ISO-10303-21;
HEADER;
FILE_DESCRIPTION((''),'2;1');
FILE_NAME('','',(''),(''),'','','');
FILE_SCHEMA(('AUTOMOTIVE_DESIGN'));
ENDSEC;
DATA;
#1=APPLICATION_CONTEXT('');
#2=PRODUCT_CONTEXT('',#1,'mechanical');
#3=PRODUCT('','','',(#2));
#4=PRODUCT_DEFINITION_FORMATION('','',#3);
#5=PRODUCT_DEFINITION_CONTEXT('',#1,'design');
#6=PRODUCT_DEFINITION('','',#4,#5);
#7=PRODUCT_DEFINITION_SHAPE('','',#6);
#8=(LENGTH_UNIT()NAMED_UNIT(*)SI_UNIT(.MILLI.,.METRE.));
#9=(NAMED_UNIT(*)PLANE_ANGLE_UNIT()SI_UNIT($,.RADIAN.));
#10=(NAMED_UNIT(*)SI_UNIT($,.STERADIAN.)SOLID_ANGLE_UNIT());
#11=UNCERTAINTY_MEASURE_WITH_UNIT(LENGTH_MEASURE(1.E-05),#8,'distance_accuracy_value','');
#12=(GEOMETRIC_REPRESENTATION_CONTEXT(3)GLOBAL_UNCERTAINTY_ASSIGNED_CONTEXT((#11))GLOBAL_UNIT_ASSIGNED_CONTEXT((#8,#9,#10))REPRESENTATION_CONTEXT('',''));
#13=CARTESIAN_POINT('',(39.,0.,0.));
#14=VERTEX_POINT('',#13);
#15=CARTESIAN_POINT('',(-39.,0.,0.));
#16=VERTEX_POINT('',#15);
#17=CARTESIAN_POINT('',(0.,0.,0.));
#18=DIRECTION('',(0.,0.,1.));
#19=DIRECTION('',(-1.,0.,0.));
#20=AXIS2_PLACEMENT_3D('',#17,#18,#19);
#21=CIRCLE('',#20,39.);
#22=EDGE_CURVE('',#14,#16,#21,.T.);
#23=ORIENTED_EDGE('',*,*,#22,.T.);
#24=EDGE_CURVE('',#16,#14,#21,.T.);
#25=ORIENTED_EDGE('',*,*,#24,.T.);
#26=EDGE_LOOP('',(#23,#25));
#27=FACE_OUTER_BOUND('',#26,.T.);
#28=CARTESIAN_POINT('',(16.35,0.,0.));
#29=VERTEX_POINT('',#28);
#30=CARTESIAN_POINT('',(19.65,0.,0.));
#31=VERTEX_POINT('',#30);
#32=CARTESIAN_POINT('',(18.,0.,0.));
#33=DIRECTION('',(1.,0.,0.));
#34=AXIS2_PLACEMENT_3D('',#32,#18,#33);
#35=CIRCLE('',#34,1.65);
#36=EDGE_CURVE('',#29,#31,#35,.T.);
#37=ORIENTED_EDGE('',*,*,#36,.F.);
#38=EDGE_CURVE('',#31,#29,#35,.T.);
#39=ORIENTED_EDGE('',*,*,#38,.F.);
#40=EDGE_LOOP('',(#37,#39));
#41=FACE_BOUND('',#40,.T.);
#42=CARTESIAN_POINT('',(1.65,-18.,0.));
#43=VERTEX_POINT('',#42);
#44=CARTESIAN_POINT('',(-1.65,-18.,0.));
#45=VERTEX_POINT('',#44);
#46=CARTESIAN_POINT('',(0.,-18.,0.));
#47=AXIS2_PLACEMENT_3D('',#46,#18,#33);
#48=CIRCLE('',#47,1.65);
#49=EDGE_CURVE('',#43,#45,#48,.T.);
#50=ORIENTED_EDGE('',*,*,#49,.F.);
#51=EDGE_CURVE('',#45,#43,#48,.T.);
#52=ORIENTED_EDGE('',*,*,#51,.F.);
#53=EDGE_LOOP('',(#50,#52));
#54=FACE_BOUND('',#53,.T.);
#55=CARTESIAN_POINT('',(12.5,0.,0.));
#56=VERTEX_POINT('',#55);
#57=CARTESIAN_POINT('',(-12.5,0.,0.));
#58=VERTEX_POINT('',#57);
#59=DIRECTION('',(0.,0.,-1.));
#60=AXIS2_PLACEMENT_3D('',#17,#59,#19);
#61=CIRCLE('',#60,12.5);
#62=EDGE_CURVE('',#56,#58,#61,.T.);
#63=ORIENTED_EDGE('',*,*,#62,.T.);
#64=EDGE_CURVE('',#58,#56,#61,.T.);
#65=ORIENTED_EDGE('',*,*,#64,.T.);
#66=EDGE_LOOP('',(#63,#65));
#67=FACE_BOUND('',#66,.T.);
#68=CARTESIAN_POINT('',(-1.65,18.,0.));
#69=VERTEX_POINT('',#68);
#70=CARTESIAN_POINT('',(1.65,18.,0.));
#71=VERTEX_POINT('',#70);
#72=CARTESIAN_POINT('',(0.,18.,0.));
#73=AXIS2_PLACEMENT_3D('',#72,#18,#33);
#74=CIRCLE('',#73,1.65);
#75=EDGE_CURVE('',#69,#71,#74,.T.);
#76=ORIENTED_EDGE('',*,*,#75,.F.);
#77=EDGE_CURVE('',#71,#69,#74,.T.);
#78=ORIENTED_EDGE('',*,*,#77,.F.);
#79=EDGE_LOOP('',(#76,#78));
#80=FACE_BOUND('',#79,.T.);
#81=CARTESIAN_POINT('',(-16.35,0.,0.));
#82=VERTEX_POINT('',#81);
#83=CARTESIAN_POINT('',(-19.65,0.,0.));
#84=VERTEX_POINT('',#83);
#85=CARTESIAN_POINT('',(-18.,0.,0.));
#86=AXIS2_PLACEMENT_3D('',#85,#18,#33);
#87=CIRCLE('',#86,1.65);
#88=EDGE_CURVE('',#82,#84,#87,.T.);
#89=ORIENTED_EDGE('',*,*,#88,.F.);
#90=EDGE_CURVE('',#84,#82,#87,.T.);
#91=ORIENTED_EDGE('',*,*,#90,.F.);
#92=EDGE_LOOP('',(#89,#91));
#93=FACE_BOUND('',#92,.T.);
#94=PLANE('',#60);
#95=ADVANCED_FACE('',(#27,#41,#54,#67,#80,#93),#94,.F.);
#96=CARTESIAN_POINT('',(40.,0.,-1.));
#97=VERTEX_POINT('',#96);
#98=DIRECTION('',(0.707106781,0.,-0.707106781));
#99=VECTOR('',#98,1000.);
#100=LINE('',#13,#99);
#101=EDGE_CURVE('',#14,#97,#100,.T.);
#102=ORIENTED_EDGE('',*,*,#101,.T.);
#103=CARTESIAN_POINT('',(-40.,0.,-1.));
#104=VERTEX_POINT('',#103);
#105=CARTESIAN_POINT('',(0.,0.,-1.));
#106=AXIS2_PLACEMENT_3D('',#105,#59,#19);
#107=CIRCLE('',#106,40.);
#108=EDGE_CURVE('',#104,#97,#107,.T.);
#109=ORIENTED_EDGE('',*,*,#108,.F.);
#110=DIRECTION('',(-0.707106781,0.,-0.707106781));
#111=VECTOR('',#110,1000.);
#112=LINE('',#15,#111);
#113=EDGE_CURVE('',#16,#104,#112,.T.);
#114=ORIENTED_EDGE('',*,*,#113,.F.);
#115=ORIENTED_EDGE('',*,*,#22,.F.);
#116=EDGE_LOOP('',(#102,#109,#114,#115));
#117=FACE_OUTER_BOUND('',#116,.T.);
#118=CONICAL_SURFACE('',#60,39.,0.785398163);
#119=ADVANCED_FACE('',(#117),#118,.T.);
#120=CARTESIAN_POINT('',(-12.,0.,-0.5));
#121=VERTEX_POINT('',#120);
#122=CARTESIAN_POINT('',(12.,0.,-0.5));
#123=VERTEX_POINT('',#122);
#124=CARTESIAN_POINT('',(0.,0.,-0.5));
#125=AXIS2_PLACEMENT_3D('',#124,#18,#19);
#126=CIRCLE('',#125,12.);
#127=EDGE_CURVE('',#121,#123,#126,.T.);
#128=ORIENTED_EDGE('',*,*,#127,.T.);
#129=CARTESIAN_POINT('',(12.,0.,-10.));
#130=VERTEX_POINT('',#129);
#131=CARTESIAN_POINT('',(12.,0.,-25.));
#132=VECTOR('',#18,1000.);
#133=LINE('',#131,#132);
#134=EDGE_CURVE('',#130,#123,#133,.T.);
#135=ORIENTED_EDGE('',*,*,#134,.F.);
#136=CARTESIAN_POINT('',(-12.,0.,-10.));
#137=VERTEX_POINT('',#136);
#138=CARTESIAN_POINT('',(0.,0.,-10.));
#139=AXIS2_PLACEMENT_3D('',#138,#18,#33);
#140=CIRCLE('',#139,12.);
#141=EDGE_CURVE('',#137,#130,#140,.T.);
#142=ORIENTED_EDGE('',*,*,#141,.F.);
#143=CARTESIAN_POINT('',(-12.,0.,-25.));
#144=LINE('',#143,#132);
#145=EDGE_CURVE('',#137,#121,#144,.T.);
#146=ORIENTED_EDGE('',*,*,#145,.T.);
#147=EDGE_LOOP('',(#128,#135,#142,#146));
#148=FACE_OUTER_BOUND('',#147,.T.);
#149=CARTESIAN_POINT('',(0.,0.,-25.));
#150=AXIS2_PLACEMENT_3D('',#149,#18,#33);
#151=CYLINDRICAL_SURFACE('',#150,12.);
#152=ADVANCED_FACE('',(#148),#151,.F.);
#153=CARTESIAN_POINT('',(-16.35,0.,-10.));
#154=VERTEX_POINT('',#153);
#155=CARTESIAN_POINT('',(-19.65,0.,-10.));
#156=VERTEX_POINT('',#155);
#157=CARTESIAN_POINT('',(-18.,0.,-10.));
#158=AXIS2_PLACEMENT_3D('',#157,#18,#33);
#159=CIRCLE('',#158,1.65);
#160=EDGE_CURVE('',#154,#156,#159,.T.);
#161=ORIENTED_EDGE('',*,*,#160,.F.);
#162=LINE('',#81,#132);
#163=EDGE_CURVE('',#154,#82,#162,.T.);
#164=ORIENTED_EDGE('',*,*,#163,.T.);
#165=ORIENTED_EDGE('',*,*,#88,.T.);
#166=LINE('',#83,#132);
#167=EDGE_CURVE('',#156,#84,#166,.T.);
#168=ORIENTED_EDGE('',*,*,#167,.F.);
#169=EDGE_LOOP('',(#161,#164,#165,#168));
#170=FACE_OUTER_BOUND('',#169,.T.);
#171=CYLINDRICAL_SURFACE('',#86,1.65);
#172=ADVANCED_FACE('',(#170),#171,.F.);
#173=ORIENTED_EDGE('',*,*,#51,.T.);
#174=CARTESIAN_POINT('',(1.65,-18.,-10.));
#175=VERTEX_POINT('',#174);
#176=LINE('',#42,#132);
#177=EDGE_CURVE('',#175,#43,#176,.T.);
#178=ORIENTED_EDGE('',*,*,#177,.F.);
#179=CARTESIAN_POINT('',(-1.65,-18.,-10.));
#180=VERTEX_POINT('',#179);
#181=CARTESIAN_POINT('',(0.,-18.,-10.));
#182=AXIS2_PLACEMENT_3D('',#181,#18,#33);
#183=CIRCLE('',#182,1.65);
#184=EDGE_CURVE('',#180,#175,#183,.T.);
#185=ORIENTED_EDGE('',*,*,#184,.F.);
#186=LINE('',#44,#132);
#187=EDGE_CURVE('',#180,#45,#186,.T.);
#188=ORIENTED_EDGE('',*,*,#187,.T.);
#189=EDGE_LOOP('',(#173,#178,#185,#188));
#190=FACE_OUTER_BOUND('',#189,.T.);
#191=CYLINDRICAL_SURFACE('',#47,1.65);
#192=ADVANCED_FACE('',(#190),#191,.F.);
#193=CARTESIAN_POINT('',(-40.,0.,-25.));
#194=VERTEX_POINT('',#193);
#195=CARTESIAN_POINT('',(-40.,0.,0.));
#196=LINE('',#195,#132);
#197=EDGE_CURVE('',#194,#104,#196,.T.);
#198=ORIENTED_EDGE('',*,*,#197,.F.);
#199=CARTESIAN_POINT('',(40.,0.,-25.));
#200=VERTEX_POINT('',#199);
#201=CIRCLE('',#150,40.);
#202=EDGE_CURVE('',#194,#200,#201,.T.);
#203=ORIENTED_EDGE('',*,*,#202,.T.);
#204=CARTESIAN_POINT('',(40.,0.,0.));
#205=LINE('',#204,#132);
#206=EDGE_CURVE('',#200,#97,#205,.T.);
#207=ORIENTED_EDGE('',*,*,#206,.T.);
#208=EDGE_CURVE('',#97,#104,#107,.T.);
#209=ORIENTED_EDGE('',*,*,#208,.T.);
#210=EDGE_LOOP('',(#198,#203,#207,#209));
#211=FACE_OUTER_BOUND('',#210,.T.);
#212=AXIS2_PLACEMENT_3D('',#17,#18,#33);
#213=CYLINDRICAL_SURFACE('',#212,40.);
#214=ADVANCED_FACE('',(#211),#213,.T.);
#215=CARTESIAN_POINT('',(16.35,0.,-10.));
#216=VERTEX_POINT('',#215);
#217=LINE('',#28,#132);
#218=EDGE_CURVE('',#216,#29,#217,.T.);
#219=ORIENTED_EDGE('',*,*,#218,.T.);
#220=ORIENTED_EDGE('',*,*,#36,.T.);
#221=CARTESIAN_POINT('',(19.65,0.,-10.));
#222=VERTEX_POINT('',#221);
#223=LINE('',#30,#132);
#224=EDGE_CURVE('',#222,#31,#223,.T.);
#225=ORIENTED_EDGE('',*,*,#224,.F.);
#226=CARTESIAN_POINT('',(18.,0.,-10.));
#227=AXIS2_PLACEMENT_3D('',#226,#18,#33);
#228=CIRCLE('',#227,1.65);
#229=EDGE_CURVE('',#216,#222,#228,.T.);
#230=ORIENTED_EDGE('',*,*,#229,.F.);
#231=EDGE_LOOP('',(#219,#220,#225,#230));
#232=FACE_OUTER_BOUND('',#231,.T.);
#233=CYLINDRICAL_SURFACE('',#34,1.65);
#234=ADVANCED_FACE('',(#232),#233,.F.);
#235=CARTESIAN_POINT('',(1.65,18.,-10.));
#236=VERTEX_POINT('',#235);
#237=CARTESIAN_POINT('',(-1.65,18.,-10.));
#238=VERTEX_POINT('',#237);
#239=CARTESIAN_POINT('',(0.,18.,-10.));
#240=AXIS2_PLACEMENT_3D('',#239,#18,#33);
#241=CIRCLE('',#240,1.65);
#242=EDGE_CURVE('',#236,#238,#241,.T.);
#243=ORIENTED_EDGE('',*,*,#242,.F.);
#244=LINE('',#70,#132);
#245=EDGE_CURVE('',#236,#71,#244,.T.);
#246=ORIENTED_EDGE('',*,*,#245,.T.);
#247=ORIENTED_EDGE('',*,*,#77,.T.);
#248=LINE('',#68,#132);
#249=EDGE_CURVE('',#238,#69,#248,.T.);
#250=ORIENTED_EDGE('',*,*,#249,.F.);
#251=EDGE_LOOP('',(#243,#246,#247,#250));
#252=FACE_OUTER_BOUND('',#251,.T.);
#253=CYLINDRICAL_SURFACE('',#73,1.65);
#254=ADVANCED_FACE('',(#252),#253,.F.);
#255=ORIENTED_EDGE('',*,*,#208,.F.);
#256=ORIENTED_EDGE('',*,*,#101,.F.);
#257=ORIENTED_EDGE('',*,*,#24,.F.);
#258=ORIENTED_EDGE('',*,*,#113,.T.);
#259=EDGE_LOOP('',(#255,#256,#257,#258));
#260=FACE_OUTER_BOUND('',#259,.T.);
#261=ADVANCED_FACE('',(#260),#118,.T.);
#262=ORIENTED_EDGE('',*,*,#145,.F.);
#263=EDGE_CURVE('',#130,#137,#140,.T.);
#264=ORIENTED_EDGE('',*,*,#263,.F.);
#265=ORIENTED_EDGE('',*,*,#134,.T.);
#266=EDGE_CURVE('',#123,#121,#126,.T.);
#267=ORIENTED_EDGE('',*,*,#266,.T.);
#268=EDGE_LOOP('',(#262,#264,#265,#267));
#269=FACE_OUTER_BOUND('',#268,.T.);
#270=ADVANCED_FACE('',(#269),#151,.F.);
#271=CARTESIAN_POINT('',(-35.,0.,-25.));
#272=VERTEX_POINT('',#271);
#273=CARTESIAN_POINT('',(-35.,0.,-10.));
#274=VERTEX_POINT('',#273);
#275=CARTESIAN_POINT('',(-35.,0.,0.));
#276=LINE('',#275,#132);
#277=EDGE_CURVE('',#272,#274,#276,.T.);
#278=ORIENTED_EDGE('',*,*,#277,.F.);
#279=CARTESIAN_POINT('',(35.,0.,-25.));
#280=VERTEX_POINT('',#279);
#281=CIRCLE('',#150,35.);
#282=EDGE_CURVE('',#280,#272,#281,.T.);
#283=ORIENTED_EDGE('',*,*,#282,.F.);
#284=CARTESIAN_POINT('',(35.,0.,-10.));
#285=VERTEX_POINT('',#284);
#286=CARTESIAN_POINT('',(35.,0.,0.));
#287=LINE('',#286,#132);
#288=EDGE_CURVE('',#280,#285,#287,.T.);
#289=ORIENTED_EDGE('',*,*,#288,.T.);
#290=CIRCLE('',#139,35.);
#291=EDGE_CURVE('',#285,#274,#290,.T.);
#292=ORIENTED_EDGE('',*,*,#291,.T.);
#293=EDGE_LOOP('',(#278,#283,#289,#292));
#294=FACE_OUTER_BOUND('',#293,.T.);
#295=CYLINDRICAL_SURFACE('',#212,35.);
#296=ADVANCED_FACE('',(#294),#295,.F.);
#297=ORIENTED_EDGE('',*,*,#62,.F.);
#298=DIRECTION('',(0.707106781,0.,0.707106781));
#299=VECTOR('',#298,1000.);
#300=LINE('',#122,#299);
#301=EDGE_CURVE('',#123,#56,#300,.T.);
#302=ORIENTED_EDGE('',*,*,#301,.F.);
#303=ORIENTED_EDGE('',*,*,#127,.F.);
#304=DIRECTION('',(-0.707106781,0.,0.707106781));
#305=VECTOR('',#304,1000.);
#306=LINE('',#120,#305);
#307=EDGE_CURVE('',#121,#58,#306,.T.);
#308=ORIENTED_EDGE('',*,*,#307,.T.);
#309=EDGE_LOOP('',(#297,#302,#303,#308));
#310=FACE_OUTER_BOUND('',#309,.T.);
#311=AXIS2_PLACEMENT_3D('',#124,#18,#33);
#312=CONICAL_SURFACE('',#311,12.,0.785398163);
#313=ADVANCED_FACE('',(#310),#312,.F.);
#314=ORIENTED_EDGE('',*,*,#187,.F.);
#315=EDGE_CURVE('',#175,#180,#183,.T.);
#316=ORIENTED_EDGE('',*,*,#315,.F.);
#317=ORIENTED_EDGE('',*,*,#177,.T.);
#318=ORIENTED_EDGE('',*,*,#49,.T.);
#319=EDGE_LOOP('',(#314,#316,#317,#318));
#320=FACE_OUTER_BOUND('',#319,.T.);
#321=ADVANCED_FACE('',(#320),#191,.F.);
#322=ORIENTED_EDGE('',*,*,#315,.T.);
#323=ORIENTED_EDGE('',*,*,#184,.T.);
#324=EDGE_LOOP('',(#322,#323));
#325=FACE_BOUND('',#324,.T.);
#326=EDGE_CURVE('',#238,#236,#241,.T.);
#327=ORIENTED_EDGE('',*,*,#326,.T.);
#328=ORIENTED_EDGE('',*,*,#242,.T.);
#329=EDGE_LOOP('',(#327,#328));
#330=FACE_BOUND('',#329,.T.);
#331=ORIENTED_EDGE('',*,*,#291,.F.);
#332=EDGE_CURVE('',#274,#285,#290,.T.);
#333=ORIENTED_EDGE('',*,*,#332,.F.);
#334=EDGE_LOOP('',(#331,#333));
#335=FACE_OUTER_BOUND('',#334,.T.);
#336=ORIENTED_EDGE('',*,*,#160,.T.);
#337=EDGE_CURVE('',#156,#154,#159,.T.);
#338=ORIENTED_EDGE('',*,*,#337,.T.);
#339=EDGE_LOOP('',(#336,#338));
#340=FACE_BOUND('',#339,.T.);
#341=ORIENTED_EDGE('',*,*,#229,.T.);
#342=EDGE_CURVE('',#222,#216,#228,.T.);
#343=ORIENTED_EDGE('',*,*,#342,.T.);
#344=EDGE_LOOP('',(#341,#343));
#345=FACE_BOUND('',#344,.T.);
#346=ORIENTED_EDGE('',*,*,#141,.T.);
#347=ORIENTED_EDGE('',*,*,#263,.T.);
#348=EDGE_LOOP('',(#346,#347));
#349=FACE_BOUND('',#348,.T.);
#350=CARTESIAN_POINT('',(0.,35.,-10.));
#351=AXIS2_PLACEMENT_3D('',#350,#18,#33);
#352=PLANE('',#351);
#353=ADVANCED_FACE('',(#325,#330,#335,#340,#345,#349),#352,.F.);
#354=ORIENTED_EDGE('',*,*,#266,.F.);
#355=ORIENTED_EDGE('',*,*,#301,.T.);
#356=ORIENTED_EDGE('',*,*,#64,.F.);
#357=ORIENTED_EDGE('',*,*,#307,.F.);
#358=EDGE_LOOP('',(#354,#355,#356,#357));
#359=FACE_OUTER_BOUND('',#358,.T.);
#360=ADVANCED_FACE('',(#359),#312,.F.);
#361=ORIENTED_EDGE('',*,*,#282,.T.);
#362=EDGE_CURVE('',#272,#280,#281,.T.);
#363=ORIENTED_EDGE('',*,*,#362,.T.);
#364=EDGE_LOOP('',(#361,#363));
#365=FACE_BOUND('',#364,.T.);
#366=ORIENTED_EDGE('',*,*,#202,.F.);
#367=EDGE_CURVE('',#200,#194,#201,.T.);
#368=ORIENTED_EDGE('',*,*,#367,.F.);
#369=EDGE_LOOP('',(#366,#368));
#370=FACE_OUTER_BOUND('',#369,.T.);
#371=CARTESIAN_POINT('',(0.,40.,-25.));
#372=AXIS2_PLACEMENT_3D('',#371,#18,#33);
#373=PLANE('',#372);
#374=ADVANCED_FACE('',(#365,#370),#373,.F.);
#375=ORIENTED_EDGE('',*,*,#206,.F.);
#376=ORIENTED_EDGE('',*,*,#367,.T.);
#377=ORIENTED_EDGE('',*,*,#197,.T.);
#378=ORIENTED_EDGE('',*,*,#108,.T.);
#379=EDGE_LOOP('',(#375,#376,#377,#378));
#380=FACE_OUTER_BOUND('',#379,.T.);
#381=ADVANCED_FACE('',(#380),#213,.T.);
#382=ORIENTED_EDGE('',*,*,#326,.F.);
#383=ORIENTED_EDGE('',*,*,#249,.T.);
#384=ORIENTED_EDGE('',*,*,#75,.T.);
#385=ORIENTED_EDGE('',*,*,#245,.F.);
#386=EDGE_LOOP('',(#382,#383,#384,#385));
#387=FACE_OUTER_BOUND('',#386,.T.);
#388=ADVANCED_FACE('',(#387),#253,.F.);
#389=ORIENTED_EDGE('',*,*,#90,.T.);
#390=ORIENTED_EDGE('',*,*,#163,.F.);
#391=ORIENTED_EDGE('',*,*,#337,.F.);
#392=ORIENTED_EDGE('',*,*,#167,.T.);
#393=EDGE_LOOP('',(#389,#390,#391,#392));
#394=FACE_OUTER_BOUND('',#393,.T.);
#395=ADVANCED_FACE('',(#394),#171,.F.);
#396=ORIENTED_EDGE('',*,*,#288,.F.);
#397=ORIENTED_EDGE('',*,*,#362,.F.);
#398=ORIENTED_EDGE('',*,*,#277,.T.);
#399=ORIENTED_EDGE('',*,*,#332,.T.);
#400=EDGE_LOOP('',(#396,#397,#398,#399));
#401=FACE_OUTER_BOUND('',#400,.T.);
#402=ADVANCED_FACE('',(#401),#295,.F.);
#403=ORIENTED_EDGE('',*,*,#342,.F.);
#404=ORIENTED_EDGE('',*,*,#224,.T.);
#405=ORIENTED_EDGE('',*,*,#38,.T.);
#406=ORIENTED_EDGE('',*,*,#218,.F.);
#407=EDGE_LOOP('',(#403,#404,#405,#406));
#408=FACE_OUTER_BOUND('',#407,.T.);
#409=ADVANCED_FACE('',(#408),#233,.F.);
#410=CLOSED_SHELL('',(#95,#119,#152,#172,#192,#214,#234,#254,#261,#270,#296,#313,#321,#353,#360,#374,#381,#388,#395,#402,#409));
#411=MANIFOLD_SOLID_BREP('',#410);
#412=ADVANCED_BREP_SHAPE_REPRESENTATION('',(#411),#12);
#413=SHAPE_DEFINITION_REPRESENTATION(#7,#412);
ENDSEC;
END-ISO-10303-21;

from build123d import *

# Parameters (mm, degrees)
CHAMFER1_SIZE      = 1
SKETCH9_R          = 12
CUT_EXTRUDE1_DEPTH = 62.846584384
M4_TAPPED_HOLE1_D  = 3.3
CHAMFER2_SIZE      = 0.5


with BuildPart() as part:
    # Sketch8 → Revolve2 (revolve)
    with BuildSketch(Plane(origin=(0, 0, 0), x_dir=(0, 0, -1), z_dir=(1, 0, 0)), mode=Mode.PRIVATE) as revolve2_sk:
        Polygon((0, 0), (0, 40), (25, 40), (25, 35), (10, 35), (10, 0), align=None)
    revolve(revolve2_sk.sketch.rotate(Axis((0, 0, 0), (0, 0, -1)), 90), axis=Axis((0, 0, 0), (0, 0, -1)))

    # Chamfer1
    chamfer1_edges = [part.edges().sort_by_distance(p)[0] for p in [
        (-40, 0, 0),
    ]]
    chamfer(chamfer1_edges, length=CHAMFER1_SIZE)

    # Sketch9 → Cut-Extrude1 (cut, through all)
    with BuildSketch(Plane.XY):
        Circle(SKETCH9_R)
    extrude(amount=-CUT_EXTRUDE1_DEPTH, mode=Mode.SUBTRACT)

    # M4 Tapped Hole1 (through all)
    with Locations(Plane(origin=(0, 18, 0), x_dir=(1, 0, 0), z_dir=(0, 0, 1))):
        with Locations((0, 0), (-18, -18), (18, -18), (0, -36)):
            Hole(M4_TAPPED_HOLE1_D / 2)

    # Chamfer2
    chamfer2_edges = [part.edges().sort_by_distance(p)[0] for p in [
        (-12, 0, 0),
    ]]
    chamfer(chamfer2_edges, length=CHAMFER2_SIZE)


solid = part.part
